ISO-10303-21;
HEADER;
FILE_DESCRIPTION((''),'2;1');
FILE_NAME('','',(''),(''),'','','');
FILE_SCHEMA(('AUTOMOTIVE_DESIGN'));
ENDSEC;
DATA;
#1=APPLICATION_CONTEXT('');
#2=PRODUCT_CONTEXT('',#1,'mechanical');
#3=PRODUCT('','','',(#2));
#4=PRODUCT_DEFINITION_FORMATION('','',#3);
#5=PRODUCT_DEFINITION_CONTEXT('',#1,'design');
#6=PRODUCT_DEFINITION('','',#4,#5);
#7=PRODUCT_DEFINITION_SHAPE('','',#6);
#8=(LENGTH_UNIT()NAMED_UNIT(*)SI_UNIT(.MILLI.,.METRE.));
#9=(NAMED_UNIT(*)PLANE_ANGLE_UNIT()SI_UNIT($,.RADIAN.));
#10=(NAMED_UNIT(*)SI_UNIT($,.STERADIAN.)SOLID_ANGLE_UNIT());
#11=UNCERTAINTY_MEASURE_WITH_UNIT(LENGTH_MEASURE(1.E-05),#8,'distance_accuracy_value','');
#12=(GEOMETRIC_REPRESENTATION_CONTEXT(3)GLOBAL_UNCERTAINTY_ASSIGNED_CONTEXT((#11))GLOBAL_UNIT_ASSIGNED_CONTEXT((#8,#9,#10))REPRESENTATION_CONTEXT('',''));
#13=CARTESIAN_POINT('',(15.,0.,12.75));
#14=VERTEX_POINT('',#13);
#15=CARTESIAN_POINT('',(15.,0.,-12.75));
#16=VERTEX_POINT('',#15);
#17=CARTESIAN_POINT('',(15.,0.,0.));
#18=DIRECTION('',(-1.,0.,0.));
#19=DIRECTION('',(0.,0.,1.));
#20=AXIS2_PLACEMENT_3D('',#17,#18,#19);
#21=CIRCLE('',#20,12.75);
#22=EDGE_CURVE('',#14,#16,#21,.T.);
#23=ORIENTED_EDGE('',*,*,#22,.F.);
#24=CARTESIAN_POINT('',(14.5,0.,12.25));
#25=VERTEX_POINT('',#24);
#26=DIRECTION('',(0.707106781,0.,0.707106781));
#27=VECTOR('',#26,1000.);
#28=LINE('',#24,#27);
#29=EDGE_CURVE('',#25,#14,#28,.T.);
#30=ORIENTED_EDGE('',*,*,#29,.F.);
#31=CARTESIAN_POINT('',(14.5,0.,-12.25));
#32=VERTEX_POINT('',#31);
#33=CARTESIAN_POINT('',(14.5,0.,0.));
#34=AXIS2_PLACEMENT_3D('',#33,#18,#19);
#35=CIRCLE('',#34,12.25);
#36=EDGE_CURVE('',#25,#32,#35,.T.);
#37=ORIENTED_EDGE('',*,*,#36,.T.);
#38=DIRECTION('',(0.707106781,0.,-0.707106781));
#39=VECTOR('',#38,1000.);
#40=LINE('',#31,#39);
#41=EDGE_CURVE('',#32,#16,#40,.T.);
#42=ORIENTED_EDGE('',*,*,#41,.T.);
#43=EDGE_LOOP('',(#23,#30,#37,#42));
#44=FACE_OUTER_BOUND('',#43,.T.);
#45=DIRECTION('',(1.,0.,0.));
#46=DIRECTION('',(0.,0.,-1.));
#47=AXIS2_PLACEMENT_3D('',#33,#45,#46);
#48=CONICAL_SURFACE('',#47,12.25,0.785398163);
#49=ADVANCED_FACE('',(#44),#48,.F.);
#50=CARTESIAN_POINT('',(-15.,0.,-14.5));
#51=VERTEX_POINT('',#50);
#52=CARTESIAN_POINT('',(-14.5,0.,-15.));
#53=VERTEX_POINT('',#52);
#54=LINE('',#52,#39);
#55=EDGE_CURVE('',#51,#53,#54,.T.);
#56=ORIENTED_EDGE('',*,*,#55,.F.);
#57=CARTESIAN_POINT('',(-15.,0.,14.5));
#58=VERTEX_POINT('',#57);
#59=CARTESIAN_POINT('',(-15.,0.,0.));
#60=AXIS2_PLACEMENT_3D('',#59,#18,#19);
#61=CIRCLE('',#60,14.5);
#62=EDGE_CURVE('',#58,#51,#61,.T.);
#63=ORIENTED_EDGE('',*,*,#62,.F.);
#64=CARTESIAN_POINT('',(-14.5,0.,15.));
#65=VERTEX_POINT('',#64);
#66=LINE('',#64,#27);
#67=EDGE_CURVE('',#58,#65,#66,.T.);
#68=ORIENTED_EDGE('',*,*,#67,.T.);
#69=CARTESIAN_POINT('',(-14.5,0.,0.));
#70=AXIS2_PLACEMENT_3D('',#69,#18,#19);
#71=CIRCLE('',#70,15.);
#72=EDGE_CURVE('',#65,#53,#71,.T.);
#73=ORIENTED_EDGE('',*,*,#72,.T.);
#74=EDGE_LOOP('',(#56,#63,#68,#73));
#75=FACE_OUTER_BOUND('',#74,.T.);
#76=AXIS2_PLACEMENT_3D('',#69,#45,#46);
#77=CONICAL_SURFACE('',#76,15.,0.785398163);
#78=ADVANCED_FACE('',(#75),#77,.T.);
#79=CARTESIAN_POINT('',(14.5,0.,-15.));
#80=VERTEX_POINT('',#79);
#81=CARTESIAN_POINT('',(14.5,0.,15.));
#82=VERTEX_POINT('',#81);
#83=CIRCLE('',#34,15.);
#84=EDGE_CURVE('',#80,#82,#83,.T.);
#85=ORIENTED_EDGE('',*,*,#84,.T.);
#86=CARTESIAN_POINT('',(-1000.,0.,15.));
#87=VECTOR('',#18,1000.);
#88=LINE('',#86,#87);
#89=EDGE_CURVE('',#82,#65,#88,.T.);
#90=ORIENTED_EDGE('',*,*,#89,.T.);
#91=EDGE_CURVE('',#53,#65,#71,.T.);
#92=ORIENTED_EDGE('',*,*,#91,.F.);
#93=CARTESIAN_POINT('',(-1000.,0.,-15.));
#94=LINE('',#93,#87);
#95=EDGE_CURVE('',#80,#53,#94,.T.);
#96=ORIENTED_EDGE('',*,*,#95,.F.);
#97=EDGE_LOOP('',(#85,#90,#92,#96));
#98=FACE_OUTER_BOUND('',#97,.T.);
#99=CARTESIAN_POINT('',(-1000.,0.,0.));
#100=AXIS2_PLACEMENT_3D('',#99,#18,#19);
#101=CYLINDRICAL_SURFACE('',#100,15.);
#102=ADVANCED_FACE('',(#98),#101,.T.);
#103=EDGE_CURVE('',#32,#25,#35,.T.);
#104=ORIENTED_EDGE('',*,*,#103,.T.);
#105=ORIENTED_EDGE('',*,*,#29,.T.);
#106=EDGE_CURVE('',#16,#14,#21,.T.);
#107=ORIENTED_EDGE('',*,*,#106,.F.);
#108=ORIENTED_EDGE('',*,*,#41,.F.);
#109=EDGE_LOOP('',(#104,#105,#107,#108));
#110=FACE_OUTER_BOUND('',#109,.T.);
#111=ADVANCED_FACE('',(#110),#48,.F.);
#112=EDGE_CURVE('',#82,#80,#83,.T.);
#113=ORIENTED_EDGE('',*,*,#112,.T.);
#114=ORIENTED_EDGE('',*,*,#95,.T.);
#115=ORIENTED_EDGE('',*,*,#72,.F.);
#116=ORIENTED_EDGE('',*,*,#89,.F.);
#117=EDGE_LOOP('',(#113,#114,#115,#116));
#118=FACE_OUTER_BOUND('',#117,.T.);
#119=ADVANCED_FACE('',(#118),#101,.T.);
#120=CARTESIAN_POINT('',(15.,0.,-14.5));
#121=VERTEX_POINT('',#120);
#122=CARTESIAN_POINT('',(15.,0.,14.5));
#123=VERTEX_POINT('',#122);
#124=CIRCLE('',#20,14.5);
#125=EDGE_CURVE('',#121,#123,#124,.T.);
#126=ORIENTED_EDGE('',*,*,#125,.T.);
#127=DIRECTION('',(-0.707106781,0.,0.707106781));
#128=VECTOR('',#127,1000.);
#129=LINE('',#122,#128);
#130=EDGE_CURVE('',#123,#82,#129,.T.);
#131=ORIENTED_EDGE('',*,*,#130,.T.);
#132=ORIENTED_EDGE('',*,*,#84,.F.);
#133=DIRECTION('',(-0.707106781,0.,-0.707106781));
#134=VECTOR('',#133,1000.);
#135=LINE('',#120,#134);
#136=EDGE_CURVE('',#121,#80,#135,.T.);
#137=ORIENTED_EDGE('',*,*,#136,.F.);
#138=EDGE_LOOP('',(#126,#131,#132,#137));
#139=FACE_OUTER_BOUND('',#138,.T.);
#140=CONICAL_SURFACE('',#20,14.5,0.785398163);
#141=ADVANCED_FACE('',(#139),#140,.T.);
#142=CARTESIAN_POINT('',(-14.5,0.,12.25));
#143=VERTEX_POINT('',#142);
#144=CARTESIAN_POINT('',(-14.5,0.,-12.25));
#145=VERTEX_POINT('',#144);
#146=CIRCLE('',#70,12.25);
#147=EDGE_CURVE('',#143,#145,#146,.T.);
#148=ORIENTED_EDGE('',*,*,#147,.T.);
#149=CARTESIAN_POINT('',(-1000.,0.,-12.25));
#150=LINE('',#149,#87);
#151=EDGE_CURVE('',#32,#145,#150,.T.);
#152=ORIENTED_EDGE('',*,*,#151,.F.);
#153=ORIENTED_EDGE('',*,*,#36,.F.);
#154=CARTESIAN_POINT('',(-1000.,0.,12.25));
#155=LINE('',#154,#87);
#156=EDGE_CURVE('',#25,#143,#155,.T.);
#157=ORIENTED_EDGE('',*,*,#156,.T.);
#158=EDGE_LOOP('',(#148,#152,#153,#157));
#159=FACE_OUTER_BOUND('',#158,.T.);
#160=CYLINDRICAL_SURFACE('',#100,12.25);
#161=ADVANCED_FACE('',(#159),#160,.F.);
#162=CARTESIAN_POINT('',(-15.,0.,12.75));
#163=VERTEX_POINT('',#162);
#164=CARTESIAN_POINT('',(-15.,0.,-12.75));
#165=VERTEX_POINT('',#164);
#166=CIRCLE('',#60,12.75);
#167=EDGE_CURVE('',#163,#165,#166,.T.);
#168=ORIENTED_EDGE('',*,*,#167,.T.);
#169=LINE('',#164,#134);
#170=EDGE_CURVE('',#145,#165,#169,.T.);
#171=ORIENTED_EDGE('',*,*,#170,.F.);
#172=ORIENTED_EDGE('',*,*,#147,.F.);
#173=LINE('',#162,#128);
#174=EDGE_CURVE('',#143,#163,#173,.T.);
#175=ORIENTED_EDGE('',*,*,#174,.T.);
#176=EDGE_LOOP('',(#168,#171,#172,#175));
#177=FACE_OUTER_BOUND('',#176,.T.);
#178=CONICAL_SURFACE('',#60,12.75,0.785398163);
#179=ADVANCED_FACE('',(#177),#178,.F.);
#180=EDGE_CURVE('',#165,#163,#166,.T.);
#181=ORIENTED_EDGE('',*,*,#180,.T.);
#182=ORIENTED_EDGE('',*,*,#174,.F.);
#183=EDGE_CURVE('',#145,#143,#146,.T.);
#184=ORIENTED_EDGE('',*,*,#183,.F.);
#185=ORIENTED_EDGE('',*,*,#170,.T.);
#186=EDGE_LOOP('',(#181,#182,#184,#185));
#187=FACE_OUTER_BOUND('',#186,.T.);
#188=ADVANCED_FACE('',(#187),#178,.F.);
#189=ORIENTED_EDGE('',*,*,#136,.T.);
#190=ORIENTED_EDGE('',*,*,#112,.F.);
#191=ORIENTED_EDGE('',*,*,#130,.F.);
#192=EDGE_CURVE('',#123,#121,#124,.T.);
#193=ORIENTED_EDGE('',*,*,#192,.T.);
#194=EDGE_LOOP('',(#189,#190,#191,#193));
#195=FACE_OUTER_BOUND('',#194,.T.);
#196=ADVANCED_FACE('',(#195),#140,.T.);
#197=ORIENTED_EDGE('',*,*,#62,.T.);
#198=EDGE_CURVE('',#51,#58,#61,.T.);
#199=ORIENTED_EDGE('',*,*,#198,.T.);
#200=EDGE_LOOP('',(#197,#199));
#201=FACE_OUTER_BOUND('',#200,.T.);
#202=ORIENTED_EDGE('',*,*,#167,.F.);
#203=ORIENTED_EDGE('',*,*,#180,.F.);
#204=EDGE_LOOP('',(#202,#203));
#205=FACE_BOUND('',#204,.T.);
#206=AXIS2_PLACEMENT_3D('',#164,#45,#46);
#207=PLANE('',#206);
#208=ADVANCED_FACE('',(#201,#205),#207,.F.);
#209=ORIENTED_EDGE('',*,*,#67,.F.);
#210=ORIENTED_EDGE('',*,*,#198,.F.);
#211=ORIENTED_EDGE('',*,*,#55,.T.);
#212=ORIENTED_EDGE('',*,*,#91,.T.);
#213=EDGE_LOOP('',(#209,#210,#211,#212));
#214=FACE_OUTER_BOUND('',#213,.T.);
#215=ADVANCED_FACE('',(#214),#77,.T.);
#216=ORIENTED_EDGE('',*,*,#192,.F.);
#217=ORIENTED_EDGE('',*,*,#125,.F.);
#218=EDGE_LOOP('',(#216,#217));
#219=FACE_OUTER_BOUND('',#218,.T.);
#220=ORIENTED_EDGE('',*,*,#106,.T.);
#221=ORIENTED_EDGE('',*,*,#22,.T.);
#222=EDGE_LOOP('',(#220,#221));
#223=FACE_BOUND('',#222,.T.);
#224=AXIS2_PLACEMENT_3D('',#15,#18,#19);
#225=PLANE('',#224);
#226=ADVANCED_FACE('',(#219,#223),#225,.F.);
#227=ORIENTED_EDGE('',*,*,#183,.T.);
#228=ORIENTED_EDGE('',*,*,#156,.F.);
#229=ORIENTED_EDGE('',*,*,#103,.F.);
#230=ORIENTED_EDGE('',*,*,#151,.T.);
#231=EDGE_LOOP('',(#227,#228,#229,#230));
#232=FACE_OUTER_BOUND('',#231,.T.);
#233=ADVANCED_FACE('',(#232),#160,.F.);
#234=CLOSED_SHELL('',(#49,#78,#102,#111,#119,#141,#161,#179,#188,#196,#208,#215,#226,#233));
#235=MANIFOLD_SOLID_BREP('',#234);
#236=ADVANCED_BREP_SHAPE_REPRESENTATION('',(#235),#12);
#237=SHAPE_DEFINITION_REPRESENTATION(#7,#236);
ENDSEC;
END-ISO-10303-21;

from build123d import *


with BuildPart() as part:
    # 草图1 → 旋转1 (revolve)
    with BuildSketch(Plane(origin=(0, 0, 0), x_dir=(1, 0, 0), z_dir=(0, 1, 0)), mode=Mode.PRIVATE) as revolve_1_sk:
        Polygon((-15, 14.5), (-14.5, 15), (14.5, 15), (15, 14.5), (15, 12.75), (14.5, 12.25), (-14.5, 12.25), (-15, 12.75), align=None)
    revolve(revolve_1_sk.sketch.rotate(Axis((-1000, 0, 0), (1, 0, 0)), 180), axis=Axis((-1000, 0, 0), (1, 0, 0)))


solid = part.part
